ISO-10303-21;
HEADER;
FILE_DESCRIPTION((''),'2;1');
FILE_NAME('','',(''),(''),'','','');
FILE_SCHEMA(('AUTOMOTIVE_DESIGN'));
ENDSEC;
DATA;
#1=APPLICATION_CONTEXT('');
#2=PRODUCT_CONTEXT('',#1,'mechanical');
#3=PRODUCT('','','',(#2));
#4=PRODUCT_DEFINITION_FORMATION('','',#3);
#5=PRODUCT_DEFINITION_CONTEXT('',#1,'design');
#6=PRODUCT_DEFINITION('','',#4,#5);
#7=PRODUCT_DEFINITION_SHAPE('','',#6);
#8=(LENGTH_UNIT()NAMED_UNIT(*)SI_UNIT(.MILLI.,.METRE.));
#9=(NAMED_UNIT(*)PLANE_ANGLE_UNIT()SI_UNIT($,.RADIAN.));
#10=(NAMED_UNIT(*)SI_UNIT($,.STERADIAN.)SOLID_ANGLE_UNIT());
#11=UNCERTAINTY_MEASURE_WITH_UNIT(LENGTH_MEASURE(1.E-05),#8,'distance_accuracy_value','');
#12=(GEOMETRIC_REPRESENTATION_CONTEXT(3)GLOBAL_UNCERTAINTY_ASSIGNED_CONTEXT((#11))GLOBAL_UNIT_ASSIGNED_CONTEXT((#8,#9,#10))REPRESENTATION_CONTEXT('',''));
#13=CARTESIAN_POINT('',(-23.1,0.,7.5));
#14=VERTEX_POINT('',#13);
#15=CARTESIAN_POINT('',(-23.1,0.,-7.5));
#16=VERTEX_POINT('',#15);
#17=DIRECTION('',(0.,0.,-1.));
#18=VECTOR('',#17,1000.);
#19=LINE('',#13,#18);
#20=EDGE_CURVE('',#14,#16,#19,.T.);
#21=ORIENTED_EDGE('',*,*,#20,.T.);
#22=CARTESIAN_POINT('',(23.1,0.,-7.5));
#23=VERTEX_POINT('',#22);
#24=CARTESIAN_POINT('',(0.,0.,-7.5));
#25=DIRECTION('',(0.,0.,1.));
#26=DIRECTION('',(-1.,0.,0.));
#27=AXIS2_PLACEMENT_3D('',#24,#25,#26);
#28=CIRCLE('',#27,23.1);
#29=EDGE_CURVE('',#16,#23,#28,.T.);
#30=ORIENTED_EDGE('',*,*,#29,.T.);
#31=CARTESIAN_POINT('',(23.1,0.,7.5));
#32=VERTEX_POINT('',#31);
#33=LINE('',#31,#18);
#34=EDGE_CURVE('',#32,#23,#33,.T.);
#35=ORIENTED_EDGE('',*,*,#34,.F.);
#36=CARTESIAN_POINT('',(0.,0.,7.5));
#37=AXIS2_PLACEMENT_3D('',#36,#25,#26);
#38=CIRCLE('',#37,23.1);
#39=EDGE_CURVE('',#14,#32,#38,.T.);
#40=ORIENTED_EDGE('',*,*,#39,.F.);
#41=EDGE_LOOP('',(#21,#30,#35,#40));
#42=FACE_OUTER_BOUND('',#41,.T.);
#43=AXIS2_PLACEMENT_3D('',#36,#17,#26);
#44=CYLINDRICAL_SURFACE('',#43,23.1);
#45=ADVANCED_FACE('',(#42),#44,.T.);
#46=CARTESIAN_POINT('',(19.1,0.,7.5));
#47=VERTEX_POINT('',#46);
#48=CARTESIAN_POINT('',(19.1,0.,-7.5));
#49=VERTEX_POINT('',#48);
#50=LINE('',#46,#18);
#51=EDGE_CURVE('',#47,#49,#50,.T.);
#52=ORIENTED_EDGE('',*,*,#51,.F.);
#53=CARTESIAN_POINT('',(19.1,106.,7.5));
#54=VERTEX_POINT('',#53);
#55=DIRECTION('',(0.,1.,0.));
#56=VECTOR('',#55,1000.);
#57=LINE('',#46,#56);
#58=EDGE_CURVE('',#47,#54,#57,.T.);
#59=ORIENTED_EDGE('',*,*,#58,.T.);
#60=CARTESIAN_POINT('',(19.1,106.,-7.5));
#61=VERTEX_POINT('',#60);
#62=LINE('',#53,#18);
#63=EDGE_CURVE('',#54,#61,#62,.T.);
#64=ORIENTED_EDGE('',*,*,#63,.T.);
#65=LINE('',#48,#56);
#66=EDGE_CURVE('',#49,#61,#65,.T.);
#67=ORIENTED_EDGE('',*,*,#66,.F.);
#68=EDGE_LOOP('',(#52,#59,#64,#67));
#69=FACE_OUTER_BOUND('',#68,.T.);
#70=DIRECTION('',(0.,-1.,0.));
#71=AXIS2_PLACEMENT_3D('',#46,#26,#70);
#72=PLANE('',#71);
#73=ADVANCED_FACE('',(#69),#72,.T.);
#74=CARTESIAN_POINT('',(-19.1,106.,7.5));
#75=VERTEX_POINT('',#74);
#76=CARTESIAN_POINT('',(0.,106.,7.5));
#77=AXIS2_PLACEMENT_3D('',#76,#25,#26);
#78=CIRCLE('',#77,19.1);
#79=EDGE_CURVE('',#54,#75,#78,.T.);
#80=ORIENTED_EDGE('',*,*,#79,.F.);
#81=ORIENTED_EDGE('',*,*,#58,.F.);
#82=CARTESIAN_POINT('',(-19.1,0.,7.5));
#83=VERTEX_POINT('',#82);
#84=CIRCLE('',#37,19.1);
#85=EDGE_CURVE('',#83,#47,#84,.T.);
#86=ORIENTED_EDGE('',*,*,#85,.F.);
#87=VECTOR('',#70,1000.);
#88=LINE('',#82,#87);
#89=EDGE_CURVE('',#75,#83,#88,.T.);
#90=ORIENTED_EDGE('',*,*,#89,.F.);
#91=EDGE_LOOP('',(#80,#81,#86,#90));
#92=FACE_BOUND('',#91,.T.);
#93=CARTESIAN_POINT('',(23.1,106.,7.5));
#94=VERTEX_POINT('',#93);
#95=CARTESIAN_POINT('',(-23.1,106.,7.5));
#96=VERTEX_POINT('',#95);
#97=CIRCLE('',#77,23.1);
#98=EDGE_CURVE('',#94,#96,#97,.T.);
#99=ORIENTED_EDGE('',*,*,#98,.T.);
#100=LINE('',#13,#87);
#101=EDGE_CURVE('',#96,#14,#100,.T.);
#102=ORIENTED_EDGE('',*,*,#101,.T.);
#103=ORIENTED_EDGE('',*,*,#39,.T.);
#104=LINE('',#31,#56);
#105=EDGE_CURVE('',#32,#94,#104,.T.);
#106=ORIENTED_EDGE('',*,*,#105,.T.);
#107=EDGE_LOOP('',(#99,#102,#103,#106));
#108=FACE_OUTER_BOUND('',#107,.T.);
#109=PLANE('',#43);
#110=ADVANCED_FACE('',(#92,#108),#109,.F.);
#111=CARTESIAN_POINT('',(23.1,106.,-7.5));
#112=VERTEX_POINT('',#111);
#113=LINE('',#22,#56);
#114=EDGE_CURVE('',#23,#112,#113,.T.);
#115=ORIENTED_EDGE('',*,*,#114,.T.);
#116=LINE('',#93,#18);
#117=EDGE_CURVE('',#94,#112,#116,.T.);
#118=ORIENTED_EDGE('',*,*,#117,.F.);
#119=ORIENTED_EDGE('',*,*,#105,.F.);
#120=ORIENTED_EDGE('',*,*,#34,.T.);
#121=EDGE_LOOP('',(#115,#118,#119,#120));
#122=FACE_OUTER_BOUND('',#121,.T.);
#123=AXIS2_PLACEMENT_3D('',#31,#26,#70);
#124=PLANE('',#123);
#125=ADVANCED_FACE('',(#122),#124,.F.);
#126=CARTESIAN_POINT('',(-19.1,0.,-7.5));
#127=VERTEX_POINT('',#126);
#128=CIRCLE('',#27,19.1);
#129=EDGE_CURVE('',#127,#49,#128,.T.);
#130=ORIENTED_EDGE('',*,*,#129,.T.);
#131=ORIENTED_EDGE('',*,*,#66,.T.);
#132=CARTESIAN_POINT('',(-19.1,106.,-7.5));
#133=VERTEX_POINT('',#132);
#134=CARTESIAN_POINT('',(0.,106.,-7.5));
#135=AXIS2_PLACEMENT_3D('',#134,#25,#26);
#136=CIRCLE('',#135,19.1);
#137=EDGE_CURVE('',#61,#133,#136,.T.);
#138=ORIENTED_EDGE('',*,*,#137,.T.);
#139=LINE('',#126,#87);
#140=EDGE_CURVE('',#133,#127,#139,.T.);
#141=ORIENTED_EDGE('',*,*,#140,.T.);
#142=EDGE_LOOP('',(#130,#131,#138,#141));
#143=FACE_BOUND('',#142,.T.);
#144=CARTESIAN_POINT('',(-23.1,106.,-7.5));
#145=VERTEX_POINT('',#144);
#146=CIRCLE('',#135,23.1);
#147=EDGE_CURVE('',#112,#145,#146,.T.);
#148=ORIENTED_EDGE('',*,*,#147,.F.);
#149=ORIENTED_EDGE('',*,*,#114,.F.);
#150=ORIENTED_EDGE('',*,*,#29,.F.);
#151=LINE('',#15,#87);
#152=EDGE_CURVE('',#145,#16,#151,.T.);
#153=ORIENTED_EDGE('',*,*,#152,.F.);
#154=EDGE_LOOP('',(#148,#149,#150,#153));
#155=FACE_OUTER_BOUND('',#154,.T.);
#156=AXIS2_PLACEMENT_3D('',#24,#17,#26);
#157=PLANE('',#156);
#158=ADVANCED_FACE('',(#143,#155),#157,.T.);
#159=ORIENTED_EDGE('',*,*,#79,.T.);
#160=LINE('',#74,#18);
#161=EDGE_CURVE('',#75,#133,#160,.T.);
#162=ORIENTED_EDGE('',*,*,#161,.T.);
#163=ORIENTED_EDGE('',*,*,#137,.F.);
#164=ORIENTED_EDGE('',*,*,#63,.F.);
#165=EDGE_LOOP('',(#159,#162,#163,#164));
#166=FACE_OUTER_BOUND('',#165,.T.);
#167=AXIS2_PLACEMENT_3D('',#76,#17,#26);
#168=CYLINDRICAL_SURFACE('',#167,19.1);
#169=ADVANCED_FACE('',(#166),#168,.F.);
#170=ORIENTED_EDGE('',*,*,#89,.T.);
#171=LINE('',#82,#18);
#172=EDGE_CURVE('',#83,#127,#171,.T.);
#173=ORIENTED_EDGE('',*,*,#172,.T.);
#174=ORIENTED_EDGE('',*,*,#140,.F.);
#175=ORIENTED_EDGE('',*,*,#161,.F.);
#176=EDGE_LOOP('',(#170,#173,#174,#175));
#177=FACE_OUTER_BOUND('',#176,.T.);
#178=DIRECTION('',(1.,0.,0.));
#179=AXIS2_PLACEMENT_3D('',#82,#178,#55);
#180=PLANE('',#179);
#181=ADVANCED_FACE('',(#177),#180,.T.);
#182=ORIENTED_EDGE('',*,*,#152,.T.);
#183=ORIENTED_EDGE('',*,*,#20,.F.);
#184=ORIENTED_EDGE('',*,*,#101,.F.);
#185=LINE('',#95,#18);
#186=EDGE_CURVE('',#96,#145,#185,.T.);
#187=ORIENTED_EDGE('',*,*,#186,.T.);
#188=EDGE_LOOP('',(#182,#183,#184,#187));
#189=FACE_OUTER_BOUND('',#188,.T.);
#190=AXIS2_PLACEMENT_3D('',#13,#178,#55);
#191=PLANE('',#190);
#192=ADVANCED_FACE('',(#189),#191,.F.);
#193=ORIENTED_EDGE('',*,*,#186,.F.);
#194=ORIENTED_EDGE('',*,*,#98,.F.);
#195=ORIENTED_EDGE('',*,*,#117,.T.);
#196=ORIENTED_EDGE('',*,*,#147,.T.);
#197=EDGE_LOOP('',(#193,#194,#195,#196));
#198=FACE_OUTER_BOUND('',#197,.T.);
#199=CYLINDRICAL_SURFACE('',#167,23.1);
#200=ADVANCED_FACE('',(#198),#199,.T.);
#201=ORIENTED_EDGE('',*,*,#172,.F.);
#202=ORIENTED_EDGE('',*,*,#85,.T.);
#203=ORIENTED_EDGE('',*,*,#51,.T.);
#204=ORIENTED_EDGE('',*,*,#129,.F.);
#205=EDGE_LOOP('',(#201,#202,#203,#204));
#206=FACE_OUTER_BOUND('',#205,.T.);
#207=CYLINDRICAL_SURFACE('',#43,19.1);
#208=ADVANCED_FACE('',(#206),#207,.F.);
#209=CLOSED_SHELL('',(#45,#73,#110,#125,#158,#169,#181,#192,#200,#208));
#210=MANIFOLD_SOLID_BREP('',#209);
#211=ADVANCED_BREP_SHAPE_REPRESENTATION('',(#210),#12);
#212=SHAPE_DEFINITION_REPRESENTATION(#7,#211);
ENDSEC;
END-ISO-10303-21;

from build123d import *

# Parameters (mm, degrees)
EXTRUDE_1_DEPTH = 7.5


with BuildPart() as part:
    # 草图2 → 拉伸-薄壁1 (new, symmetric)
    with BuildSketch(Plane.XY):
        with BuildLine():
            Line((23.1, 106), (23.1, 0))
            ThreePointArc((23.1, 0), (0, -23.1), (-23.1, 0))
            Line((-23.1, 0), (-23.1, 106))
            ThreePointArc((-23.1, 106), (0, 129.1), (23.1, 106))
        make_face()
        with BuildLine():
            Line((19.1, 106), (19.1, 0))
            ThreePointArc((19.1, 0), (0, -19.1), (-19.1, 0))
            Line((-19.1, 0), (-19.1, 106))
            ThreePointArc((-19.1, 106), (0, 125.1), (19.1, 106))
        make_face(mode=Mode.SUBTRACT)
    extrude(amount=EXTRUDE_1_DEPTH, both=True)


solid = part.part
